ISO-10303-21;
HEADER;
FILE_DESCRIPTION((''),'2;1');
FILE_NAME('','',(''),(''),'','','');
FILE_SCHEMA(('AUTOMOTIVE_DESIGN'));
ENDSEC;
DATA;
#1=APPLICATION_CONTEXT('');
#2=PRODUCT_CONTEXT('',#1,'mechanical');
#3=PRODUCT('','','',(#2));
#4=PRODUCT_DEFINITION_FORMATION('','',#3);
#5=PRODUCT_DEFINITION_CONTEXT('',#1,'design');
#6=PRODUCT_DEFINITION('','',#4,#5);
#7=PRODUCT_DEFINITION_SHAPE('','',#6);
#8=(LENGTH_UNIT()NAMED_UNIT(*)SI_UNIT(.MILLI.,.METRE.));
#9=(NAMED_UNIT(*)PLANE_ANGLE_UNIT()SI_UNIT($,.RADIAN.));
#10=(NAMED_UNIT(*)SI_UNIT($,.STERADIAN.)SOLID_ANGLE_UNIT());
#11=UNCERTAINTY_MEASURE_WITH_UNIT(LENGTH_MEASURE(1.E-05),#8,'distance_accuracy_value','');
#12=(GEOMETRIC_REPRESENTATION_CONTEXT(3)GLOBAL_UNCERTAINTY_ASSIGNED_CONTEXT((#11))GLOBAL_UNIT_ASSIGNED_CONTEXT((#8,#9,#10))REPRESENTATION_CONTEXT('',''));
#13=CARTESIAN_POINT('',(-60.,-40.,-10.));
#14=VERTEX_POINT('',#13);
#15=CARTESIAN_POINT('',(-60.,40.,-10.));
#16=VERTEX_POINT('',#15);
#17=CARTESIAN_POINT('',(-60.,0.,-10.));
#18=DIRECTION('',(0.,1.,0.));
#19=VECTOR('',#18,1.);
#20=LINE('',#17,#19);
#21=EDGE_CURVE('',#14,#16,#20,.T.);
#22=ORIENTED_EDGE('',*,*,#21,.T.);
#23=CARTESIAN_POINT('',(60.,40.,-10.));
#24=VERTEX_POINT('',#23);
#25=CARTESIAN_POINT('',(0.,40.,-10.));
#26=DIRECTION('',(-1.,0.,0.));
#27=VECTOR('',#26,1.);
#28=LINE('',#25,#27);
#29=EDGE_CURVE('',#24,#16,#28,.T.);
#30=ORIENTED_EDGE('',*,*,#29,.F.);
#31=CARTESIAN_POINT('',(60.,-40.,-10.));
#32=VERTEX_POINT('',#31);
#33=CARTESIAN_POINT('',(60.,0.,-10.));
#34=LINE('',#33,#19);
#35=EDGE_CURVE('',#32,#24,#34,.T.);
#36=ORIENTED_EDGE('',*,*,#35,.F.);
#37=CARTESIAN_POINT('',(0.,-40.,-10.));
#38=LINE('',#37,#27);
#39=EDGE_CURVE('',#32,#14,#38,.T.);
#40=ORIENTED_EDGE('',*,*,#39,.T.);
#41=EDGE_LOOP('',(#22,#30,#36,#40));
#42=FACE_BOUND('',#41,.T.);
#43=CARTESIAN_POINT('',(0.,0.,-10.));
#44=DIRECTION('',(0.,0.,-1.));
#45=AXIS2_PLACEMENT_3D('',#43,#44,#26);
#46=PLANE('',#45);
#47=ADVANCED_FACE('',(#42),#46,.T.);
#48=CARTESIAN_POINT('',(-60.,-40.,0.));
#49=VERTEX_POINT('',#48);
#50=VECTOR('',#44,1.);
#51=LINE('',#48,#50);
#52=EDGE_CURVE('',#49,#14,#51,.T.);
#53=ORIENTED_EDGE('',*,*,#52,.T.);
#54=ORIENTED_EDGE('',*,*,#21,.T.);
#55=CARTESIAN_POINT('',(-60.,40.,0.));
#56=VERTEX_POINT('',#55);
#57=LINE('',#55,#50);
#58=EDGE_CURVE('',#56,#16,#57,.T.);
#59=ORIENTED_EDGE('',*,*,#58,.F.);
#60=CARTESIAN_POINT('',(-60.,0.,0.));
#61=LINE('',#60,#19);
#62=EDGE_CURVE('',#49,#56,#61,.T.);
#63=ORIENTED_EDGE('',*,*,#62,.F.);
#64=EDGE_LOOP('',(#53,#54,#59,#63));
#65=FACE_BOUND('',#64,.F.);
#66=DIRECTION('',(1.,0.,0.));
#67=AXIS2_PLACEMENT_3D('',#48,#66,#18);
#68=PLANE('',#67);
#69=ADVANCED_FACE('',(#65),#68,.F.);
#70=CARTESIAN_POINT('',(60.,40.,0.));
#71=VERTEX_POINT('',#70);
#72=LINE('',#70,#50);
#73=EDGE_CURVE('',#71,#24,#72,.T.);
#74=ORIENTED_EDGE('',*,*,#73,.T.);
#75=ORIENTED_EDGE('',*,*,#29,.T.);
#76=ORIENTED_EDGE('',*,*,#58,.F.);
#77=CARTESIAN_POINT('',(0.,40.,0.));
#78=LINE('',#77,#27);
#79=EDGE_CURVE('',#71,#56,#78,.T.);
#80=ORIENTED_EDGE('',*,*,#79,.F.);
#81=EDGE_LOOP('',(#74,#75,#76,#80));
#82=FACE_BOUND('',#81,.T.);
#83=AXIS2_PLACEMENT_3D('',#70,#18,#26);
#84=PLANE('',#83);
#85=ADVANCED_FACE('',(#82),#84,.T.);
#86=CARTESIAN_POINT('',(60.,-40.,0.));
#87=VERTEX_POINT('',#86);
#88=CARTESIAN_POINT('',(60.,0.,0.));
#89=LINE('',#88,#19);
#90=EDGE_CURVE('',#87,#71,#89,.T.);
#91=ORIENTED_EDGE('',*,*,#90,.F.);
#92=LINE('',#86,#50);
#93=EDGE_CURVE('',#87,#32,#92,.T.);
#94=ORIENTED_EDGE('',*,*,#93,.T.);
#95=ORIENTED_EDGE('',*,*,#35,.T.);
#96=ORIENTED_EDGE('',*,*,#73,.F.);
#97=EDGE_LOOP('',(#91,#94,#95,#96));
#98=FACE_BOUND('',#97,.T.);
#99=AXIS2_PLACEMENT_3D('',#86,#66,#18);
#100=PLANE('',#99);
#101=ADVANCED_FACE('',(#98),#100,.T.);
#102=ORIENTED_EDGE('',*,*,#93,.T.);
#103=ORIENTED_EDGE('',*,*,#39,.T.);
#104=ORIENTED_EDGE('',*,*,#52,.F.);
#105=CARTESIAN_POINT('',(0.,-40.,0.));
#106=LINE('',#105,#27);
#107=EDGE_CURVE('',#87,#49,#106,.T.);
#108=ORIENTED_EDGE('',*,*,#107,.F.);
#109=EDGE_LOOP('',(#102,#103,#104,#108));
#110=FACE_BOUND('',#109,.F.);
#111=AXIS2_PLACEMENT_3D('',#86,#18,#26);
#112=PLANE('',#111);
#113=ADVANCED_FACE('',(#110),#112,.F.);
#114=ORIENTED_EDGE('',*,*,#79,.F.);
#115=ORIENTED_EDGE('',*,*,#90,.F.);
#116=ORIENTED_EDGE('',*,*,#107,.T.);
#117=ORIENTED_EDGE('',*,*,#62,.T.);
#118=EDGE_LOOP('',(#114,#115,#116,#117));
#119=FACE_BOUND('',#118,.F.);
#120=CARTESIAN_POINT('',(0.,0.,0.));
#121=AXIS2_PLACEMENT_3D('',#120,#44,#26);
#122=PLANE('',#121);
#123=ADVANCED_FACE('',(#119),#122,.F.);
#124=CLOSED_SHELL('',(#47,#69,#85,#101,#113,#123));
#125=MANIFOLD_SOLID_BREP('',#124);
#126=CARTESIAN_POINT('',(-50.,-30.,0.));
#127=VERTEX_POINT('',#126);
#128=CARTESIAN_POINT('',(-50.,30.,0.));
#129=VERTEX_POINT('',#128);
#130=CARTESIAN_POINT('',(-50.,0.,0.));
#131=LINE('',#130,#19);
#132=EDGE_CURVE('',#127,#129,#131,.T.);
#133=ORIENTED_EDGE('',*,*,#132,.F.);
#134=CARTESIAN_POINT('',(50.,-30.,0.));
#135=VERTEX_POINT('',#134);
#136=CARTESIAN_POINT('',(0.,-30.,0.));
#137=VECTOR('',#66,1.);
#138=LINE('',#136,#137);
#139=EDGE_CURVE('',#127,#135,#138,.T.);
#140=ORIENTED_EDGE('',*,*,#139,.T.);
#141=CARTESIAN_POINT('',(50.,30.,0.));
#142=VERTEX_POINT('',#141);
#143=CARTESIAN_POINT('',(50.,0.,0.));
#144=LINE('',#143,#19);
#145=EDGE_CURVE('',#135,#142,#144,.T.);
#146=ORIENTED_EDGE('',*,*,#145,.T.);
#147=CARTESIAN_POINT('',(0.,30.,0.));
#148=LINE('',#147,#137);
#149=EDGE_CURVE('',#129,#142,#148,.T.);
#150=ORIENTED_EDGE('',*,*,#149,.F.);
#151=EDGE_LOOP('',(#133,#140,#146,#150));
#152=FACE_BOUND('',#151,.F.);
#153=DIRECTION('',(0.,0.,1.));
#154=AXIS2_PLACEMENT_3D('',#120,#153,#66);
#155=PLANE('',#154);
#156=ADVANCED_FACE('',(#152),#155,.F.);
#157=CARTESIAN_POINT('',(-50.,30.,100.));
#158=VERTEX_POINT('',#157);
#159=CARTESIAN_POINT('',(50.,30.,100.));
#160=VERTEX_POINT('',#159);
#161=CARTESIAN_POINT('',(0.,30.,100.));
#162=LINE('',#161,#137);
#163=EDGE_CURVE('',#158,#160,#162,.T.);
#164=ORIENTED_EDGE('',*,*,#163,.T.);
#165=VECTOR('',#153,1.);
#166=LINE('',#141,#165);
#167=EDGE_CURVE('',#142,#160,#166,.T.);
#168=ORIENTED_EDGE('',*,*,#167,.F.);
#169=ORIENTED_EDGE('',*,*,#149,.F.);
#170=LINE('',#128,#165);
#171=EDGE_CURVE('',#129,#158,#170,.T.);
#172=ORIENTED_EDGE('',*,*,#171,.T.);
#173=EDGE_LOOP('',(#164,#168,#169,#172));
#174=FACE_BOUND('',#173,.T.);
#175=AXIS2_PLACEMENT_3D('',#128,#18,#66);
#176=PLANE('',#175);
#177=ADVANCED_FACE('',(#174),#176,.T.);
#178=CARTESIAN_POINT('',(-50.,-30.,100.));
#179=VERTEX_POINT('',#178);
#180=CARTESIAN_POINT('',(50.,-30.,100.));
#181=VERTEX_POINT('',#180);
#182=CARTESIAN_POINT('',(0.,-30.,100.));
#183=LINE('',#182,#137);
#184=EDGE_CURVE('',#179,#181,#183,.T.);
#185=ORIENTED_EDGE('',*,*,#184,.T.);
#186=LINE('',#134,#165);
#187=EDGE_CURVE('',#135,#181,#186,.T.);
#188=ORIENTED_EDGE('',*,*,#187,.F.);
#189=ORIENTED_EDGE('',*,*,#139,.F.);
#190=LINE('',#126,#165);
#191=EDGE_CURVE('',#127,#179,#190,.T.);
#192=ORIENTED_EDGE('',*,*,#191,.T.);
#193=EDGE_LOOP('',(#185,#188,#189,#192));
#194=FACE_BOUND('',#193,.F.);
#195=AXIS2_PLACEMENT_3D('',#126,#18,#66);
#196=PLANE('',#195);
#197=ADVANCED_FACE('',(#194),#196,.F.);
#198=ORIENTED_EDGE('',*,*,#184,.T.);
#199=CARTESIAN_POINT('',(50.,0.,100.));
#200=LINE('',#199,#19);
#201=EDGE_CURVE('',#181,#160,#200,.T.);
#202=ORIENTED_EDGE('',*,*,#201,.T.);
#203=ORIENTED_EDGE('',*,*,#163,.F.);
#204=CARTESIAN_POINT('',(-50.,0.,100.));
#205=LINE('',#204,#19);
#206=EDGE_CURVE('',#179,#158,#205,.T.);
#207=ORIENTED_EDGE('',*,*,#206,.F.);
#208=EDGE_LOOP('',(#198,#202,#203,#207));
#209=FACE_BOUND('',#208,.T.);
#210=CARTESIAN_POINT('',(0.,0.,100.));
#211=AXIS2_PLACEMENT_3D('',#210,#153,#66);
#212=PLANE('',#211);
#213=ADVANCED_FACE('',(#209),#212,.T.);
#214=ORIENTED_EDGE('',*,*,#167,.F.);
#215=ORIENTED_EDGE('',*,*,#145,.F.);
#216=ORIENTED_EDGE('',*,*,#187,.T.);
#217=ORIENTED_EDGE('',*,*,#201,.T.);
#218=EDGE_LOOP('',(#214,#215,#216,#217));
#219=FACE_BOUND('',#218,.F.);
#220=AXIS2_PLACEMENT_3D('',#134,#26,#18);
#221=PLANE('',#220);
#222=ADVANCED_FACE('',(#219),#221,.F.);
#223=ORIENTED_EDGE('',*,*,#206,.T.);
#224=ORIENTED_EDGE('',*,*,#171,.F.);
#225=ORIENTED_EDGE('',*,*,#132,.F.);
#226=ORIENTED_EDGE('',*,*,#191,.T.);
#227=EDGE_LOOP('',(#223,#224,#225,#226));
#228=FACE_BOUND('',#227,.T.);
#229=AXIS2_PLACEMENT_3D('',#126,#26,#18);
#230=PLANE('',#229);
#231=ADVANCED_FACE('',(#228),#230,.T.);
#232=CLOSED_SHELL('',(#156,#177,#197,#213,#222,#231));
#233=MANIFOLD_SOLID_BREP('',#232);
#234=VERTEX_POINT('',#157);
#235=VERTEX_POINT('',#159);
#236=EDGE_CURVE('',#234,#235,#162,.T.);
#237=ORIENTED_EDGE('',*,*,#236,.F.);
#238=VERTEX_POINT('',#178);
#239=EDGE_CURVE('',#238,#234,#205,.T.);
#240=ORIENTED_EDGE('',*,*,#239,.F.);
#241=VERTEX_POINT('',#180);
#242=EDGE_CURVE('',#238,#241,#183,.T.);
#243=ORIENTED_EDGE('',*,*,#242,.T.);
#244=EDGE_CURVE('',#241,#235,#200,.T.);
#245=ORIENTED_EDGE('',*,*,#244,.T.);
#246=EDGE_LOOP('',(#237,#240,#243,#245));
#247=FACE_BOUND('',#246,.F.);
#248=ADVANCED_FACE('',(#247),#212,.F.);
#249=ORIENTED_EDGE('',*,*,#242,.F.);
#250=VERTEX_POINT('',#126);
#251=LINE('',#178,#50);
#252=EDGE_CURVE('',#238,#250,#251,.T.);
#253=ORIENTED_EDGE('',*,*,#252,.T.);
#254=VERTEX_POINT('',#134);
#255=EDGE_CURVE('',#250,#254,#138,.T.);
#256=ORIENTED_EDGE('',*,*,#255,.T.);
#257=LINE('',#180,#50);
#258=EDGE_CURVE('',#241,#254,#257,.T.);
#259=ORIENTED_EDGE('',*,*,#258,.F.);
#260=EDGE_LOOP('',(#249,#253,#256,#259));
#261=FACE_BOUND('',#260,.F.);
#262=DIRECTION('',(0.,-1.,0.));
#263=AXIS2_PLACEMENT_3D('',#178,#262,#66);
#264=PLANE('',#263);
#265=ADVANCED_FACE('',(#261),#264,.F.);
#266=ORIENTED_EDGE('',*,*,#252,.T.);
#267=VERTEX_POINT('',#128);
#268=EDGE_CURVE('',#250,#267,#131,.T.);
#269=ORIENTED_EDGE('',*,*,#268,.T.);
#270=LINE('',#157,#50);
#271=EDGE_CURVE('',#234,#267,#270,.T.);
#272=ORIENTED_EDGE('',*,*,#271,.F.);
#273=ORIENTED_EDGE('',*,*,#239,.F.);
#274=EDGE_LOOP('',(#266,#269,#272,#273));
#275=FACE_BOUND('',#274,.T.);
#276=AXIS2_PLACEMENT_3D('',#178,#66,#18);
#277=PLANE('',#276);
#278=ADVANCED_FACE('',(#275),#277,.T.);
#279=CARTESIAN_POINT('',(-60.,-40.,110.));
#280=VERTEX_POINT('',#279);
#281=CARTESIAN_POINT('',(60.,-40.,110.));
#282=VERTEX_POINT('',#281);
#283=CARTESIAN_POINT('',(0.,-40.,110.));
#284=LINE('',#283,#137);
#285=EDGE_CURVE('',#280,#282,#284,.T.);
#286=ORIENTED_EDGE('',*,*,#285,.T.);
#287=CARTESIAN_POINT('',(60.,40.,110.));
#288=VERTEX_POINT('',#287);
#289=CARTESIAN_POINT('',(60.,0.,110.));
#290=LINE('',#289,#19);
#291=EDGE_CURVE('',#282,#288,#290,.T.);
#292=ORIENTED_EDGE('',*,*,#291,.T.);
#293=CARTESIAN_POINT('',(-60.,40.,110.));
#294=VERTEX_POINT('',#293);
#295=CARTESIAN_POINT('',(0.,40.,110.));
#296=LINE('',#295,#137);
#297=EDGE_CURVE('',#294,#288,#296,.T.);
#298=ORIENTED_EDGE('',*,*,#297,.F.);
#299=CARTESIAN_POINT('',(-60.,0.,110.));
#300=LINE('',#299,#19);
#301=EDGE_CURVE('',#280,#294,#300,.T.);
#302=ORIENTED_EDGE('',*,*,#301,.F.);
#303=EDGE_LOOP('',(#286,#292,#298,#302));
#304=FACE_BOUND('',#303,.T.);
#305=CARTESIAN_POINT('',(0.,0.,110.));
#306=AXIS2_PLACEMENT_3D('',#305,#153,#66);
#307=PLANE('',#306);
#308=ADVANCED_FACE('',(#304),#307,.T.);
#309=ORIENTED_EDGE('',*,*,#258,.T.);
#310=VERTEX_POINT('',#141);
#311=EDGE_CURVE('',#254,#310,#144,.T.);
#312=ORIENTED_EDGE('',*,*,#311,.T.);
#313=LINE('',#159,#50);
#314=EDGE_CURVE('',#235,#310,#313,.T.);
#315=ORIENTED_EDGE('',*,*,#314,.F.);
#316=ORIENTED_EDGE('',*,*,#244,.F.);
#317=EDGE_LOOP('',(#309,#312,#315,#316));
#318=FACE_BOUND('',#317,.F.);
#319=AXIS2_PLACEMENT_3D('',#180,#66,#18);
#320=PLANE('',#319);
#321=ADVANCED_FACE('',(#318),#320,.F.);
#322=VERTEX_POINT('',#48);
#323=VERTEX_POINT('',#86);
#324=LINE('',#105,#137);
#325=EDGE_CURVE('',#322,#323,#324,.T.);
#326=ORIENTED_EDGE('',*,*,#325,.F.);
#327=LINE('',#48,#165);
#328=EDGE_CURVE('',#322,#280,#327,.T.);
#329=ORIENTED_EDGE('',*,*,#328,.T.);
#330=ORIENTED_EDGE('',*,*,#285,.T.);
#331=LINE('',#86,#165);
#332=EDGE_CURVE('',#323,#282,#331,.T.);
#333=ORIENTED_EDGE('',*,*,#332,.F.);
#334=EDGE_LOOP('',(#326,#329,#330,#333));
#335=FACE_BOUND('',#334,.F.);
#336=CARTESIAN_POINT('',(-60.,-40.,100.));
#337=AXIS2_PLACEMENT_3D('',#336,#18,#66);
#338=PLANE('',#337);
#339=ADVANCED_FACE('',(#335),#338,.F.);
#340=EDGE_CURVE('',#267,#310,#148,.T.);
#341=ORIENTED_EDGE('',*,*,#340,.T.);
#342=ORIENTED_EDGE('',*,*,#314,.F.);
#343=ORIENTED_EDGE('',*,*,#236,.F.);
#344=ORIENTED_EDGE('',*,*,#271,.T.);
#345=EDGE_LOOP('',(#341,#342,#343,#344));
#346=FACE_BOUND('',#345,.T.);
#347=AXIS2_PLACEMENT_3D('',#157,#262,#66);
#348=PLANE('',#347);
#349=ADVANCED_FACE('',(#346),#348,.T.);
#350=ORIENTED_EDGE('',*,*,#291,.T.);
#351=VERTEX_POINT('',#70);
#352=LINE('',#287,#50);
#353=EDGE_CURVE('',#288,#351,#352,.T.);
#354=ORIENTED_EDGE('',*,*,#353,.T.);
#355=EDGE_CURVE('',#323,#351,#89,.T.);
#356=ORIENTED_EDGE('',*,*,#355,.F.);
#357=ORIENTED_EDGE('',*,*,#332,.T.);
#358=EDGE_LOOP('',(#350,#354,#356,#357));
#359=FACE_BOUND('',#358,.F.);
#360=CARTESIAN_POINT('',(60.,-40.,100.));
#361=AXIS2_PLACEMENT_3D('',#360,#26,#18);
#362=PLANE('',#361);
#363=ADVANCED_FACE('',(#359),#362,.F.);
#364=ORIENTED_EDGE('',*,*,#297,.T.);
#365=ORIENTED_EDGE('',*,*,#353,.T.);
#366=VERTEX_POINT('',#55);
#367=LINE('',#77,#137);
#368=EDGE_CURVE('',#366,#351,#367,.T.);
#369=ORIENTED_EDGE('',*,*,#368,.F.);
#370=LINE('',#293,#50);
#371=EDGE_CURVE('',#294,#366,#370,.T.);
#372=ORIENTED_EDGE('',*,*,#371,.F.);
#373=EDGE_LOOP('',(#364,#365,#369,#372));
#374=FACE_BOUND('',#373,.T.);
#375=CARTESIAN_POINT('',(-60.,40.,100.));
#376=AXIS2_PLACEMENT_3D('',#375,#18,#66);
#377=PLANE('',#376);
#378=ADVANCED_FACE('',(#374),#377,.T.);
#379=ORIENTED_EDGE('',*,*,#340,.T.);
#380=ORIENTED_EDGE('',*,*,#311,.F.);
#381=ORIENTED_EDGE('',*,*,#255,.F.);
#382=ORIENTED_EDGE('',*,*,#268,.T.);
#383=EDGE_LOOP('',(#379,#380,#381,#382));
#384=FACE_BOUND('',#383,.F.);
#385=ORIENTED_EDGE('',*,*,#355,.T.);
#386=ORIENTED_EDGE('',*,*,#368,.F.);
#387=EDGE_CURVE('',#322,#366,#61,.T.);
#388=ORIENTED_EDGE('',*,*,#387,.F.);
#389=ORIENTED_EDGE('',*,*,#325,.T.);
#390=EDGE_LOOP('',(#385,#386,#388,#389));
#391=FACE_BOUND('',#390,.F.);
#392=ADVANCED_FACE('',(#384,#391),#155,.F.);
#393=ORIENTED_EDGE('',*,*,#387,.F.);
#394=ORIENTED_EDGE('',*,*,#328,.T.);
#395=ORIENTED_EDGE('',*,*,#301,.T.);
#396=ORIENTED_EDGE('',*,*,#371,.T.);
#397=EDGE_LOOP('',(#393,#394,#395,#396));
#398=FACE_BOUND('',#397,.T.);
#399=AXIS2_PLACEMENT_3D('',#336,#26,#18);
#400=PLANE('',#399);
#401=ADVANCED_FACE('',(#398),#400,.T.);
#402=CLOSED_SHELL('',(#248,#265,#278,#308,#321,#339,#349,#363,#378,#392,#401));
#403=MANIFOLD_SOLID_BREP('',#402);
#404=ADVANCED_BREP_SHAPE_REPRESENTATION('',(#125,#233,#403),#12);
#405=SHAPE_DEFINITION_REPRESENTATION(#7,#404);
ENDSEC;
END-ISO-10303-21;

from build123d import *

# Parameters (mm, degrees)
SKETCH1_W           = 100
SKETCH1_H           = 60
BOSS_EXTRUDE1_DEPTH = 100
SKETCH2_W           = 120
SKETCH2_H           = 80
SKETCH2_W_2         = 100
SKETCH2_H_2         = 60
BOSS_EXTRUDE2_DEPTH = 100
SKETCH3_W           = 120
SKETCH3_H           = 80
BOSS_EXTRUDE3_DEPTH = 10
SKETCH4_W           = 120
SKETCH4_H           = 80
BOSS_EXTRUDE4_DEPTH = 10


with BuildPart() as part:
    # Sketch1 → Boss-Extrude1 (new body)
    with BuildSketch(Plane.XY):
        Rectangle(SKETCH1_W, SKETCH1_H)
    extrude(amount=BOSS_EXTRUDE1_DEPTH)


with BuildPart() as body_2:
    # Sketch2 → Boss-Extrude2 (new body)
    with BuildSketch(Plane.XY.offset(100)):
        Rectangle(SKETCH2_W, SKETCH2_H)
        Rectangle(SKETCH2_W_2, SKETCH2_H_2, mode=Mode.SUBTRACT)
    extrude(amount=-BOSS_EXTRUDE2_DEPTH)

    # Sketch3 → Boss-Extrude3 (add)
    with BuildSketch(Plane.XY.offset(100)):
        Rectangle(SKETCH3_W, SKETCH3_H)
    extrude(amount=BOSS_EXTRUDE3_DEPTH)


with BuildPart() as body_3:
    # Sketch4 → Boss-Extrude4 (new body)
    with BuildSketch(Plane(origin=(0, 0, 0), x_dir=(-1, 0, 0), z_dir=(0, 0, -1))):
        Rectangle(SKETCH4_W, SKETCH4_H)
    extrude(amount=BOSS_EXTRUDE4_DEPTH)


solid = Compound([part.part, body_2.part, body_3.part])
